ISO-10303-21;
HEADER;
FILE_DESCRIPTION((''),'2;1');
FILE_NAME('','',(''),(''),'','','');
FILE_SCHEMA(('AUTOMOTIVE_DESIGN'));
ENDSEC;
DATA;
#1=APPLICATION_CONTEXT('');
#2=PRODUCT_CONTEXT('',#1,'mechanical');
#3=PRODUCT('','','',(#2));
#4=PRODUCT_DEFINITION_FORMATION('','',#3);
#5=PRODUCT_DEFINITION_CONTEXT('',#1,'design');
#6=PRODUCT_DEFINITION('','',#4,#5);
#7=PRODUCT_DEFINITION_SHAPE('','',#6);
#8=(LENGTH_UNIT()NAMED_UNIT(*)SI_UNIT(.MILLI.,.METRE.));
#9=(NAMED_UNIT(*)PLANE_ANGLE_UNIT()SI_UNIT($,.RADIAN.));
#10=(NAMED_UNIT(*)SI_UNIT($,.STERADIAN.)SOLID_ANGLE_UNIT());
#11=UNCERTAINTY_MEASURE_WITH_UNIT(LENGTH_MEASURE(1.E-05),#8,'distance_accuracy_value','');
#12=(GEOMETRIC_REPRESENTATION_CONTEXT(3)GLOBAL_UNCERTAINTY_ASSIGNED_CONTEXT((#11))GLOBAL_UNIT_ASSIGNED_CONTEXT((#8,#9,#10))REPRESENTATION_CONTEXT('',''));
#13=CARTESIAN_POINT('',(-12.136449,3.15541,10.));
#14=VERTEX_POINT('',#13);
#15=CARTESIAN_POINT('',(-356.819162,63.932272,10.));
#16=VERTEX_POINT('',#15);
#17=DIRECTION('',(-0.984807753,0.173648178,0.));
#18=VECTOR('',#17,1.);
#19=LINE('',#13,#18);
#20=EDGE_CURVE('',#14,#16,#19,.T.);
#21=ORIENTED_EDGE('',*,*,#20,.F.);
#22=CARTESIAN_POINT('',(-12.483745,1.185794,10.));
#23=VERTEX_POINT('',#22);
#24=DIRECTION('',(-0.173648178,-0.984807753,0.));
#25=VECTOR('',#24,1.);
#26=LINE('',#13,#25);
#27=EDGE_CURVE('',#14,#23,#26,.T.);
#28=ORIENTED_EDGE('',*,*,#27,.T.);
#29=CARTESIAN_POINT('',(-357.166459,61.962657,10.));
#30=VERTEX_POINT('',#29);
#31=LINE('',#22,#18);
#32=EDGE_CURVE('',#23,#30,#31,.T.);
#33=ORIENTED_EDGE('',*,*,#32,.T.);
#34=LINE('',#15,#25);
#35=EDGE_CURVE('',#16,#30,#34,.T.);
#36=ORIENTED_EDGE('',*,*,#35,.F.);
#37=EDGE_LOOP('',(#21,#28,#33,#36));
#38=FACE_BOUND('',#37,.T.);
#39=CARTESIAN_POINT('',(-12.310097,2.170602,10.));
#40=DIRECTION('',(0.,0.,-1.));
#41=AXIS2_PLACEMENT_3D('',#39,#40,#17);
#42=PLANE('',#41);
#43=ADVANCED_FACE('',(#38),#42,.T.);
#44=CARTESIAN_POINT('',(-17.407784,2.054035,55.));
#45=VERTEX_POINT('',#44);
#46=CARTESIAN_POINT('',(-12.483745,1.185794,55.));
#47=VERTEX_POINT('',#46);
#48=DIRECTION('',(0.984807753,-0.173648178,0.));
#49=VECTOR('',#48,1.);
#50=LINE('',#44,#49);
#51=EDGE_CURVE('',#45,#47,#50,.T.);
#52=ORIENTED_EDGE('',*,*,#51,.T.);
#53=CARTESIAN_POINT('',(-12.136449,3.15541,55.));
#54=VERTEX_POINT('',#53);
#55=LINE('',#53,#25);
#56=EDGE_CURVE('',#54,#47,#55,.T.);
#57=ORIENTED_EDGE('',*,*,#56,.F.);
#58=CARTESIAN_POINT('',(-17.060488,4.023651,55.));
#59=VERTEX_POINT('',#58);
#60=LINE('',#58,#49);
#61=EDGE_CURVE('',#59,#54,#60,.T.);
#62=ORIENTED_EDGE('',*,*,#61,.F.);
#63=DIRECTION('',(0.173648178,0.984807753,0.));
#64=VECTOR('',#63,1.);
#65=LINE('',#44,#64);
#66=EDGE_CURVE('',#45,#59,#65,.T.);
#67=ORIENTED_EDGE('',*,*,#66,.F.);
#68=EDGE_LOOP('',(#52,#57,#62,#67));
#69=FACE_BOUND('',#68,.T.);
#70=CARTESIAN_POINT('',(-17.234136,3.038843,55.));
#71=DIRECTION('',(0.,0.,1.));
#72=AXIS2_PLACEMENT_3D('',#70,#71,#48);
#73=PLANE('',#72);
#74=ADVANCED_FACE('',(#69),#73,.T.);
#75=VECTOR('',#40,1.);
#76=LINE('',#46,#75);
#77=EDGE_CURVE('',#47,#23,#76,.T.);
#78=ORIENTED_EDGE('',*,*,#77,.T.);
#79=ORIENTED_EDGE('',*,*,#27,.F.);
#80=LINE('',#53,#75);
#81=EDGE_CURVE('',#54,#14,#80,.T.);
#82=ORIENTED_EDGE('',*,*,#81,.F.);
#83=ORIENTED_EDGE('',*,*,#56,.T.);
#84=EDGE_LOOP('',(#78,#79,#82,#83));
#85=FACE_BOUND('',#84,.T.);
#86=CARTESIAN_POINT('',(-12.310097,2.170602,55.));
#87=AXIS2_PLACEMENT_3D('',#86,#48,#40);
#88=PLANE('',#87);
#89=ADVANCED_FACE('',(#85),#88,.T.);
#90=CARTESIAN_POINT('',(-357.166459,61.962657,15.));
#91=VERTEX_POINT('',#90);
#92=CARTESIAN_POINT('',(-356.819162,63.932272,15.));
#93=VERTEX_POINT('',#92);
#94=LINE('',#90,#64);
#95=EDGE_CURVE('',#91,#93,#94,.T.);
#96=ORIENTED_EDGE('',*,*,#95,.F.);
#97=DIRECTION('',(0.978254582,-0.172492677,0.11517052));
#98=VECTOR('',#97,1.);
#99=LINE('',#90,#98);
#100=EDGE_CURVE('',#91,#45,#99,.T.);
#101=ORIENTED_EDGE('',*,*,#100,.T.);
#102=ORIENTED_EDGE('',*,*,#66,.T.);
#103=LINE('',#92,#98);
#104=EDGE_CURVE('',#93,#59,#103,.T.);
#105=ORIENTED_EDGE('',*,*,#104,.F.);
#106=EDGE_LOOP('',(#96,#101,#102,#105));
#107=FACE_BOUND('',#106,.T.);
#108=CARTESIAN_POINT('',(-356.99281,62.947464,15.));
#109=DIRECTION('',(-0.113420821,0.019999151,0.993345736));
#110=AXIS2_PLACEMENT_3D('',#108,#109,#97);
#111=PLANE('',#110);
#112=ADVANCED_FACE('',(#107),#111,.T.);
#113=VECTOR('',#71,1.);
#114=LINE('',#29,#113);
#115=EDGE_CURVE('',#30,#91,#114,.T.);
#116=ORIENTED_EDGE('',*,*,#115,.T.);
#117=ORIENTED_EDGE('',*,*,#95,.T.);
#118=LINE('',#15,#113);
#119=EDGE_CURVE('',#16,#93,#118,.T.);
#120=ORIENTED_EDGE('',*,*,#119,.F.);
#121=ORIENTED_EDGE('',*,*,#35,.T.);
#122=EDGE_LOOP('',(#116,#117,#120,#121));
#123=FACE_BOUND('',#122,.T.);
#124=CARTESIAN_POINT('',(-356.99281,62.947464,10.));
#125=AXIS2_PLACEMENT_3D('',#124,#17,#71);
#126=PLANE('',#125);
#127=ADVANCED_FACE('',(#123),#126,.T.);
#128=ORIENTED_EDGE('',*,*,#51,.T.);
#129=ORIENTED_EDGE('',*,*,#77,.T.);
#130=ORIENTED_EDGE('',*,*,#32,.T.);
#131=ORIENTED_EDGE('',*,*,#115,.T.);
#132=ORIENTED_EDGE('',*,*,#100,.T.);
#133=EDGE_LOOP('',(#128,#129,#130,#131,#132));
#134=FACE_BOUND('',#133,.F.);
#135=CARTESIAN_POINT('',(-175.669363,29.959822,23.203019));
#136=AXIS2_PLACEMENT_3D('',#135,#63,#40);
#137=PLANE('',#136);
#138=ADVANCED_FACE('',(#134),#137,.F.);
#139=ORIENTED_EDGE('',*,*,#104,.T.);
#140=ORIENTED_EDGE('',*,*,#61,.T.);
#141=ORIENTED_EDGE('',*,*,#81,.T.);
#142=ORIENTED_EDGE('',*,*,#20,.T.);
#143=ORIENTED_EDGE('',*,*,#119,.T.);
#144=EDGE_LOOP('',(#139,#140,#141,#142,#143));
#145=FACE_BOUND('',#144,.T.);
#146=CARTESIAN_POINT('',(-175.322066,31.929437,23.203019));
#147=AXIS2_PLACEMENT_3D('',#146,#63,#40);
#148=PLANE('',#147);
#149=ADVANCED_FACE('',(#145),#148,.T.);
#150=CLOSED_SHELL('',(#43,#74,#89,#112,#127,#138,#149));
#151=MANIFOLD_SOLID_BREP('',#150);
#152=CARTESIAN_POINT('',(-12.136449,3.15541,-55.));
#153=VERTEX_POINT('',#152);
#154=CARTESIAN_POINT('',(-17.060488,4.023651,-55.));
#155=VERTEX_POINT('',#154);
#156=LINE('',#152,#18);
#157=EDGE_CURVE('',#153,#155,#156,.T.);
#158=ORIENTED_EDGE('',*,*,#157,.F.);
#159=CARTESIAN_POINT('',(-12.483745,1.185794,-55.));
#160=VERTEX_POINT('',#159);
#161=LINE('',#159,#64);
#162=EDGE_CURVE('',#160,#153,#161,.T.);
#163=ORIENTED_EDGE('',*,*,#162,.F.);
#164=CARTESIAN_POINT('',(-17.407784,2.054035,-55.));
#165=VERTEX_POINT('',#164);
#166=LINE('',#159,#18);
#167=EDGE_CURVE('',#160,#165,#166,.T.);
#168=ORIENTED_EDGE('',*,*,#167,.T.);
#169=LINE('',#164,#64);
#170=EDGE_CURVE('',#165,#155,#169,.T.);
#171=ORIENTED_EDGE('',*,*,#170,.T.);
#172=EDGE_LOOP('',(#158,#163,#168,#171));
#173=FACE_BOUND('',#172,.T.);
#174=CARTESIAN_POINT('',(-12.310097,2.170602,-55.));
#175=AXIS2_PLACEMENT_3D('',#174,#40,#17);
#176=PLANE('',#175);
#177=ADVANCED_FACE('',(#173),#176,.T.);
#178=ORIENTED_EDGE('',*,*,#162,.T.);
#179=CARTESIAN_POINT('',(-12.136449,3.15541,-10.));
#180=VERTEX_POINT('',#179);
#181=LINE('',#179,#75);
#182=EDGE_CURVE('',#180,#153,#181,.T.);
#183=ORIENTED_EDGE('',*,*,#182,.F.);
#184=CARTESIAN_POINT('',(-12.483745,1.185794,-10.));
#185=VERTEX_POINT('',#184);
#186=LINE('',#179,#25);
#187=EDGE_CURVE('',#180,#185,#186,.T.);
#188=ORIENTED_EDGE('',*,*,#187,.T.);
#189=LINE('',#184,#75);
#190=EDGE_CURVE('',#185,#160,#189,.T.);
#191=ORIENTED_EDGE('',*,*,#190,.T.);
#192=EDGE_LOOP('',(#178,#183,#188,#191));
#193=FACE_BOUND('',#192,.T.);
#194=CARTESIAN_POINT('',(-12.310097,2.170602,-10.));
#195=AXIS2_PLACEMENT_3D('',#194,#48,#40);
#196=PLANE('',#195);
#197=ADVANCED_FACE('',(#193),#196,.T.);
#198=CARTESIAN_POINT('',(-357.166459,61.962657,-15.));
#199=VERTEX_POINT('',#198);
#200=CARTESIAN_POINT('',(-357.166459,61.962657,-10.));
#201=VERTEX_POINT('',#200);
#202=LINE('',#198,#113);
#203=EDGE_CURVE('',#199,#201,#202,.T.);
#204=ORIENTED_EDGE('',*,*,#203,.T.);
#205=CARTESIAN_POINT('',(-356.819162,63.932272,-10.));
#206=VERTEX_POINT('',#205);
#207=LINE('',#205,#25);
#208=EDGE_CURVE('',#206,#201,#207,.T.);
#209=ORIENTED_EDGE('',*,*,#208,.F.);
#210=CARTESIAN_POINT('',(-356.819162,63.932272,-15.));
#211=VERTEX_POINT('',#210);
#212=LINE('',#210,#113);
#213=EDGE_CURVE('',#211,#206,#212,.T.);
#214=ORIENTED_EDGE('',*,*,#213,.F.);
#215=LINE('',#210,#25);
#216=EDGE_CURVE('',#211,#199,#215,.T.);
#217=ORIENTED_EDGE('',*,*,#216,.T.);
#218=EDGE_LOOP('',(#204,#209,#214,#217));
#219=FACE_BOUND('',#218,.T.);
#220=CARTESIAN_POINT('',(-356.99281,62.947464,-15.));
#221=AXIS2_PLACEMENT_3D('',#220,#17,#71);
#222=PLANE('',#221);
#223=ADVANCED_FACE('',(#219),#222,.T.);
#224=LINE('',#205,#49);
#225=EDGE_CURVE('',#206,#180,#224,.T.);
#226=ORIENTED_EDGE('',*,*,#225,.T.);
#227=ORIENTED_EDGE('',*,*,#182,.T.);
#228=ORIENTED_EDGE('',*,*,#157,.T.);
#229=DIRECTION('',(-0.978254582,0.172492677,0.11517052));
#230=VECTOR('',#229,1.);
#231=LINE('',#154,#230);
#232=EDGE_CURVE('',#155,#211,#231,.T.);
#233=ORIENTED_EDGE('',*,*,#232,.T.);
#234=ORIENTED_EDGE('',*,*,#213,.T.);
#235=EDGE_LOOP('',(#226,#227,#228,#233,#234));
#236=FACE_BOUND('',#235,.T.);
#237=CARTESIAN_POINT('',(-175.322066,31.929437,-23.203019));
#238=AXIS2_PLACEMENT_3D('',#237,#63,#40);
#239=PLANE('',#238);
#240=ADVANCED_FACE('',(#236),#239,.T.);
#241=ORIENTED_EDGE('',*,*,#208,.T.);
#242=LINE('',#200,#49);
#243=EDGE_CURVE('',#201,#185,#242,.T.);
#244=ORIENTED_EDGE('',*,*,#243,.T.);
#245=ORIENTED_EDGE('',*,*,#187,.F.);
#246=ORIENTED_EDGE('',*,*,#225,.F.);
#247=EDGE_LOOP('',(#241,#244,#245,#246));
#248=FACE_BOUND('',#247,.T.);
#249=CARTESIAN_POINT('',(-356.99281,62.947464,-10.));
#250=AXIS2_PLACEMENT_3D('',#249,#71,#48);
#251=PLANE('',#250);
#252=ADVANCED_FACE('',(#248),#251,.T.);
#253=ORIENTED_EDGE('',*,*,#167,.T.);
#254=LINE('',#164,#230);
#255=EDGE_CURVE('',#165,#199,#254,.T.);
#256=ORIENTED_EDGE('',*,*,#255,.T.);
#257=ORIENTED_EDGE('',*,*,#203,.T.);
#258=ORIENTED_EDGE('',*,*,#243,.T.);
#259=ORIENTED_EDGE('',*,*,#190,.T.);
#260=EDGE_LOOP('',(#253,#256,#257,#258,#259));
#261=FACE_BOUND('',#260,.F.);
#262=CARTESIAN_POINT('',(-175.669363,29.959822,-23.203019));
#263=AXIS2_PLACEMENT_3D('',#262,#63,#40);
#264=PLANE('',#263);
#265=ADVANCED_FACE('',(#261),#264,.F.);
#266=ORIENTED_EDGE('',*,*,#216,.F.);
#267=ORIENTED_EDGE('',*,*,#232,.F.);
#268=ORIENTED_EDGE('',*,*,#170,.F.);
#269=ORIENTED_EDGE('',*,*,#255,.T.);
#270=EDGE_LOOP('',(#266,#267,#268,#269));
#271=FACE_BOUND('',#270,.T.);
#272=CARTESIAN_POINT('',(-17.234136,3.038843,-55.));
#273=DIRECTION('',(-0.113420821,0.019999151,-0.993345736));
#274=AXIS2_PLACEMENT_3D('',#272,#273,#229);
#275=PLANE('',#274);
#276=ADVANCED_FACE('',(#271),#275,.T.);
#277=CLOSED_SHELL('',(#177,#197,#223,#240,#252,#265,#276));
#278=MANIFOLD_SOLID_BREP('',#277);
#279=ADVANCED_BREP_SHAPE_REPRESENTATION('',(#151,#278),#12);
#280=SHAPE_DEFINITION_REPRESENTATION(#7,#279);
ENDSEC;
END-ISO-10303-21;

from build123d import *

# Parameters (mm, degrees)
BOSS_EXTRUDE1_DEPTH   = 1
BOSS_EXTRUDE1_2_DEPTH = 1


with BuildPart() as part:
    # Sketch1 → Boss-Extrude1 (new, symmetric)
    with BuildSketch(Plane(origin=(0, 0, 0), x_dir=(0, 0, -1), z_dir=(0.17364817766693072, 0.984807753012208, 0))):
        Polygon((10, 12.5), (55, 12.5), (55, 17.5), (15, 362.5), (10, 362.5), align=None)
    extrude(amount=BOSS_EXTRUDE1_DEPTH, both=True)


with BuildPart() as body_2:
    # Sketch1 → Boss-Extrude1 2 (new, symmetric)
    with BuildSketch(Plane(origin=(0, 0, 0), x_dir=(0, 0, -1), z_dir=(0.17364817766693072, 0.984807753012208, 0))):
        Polygon((-10, 362.5), (-15, 362.5), (-55, 17.5), (-55, 12.5), (-10, 12.5), align=None)
    extrude(amount=BOSS_EXTRUDE1_2_DEPTH, both=True)


solid = Compound([part.part, body_2.part])
